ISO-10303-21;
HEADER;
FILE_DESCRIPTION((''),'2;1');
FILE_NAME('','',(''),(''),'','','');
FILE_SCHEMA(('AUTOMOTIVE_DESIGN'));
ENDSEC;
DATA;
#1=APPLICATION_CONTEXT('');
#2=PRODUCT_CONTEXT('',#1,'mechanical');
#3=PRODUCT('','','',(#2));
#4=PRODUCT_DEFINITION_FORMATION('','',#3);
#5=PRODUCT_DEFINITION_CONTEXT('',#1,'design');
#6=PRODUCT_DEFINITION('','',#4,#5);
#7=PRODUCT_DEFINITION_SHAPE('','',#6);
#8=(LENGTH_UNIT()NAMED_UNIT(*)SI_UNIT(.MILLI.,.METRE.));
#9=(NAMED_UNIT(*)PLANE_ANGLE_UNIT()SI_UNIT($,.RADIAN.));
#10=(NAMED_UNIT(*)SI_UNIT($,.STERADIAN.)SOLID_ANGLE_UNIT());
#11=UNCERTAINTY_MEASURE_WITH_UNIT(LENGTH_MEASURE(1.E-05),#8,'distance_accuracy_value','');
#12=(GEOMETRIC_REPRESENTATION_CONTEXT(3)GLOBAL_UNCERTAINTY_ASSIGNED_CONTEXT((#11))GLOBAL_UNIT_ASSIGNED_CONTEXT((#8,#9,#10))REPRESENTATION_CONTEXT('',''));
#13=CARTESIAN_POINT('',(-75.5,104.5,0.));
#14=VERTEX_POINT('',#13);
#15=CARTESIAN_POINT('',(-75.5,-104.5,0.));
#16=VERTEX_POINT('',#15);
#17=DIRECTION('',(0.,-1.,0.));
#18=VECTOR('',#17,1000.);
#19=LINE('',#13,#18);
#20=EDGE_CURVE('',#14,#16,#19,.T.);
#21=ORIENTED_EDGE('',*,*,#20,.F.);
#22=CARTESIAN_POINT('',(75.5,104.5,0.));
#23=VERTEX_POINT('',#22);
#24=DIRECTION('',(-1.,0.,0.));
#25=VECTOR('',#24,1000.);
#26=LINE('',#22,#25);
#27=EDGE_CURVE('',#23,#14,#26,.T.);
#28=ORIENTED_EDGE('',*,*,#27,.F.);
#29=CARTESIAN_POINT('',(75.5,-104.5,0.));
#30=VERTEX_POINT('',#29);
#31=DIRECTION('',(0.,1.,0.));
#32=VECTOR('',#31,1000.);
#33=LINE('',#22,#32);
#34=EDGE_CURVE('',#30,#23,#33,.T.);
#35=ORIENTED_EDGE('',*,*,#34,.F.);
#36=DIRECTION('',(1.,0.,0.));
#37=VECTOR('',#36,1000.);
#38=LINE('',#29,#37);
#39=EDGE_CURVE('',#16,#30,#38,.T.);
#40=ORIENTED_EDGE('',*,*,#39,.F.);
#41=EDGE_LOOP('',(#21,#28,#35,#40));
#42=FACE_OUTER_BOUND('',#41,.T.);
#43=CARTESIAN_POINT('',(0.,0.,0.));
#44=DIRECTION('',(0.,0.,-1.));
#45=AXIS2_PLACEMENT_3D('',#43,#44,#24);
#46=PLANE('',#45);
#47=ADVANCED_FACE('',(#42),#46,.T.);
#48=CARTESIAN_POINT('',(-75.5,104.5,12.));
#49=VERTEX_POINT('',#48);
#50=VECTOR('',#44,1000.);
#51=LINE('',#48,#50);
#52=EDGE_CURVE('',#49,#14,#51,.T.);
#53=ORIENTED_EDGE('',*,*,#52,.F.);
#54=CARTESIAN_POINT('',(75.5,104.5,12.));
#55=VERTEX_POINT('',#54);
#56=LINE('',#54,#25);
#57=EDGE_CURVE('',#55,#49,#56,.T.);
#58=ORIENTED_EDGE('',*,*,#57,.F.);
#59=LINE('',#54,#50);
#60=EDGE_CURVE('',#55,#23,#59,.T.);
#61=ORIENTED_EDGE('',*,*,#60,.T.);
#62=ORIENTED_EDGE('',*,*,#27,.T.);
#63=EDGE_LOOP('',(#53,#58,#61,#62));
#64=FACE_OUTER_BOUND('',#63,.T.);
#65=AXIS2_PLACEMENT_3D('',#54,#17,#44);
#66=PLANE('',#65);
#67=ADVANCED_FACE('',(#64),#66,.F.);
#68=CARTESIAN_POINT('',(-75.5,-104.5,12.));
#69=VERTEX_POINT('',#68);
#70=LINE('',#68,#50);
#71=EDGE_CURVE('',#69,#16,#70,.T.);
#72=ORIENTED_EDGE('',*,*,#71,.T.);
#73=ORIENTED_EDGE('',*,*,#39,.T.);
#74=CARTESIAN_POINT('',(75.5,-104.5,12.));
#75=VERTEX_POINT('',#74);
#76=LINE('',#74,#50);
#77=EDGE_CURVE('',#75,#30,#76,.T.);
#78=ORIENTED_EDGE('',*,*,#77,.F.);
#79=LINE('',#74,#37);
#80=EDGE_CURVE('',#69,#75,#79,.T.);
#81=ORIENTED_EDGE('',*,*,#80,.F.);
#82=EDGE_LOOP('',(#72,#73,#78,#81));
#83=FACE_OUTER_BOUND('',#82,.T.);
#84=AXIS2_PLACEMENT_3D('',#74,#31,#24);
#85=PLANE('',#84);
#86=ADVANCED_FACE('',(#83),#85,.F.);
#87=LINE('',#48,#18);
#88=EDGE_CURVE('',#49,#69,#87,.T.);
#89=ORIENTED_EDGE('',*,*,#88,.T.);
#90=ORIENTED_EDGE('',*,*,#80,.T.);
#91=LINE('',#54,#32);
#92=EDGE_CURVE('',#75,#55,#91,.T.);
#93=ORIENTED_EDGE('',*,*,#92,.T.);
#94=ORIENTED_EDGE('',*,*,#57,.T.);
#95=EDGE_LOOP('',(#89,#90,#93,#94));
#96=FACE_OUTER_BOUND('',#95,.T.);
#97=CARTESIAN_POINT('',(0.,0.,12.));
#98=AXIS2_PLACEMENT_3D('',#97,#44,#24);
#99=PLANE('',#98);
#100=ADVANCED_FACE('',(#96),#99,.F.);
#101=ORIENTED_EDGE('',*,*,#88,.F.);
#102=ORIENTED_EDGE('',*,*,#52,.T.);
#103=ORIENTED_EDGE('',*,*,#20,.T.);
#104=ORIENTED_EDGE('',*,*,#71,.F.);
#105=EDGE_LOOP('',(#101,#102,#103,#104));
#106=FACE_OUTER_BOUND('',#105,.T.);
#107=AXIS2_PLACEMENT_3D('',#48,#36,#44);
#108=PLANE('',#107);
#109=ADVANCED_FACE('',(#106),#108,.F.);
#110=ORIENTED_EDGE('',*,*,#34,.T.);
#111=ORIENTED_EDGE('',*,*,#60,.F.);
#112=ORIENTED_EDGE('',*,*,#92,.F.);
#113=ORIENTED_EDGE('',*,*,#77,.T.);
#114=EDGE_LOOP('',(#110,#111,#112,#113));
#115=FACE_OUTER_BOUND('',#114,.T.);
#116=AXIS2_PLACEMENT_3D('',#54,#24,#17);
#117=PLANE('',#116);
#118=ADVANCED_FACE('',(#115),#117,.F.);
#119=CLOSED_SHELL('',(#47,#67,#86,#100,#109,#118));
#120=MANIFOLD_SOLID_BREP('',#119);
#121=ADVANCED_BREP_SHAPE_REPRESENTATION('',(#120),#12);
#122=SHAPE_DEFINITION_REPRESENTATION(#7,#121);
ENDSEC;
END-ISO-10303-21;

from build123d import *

# Parameters (mm, degrees)
SKETCH_1_W      = 151
SKETCH_1_H      = 209
EXTRUDE_1_DEPTH = 12


with BuildPart() as part:
    # 草图1 → 凸台-拉伸1 (new body)
    with BuildSketch(Plane.XY):
        Rectangle(SKETCH_1_W, SKETCH_1_H)
    extrude(amount=EXTRUDE_1_DEPTH)


solid = part.part
